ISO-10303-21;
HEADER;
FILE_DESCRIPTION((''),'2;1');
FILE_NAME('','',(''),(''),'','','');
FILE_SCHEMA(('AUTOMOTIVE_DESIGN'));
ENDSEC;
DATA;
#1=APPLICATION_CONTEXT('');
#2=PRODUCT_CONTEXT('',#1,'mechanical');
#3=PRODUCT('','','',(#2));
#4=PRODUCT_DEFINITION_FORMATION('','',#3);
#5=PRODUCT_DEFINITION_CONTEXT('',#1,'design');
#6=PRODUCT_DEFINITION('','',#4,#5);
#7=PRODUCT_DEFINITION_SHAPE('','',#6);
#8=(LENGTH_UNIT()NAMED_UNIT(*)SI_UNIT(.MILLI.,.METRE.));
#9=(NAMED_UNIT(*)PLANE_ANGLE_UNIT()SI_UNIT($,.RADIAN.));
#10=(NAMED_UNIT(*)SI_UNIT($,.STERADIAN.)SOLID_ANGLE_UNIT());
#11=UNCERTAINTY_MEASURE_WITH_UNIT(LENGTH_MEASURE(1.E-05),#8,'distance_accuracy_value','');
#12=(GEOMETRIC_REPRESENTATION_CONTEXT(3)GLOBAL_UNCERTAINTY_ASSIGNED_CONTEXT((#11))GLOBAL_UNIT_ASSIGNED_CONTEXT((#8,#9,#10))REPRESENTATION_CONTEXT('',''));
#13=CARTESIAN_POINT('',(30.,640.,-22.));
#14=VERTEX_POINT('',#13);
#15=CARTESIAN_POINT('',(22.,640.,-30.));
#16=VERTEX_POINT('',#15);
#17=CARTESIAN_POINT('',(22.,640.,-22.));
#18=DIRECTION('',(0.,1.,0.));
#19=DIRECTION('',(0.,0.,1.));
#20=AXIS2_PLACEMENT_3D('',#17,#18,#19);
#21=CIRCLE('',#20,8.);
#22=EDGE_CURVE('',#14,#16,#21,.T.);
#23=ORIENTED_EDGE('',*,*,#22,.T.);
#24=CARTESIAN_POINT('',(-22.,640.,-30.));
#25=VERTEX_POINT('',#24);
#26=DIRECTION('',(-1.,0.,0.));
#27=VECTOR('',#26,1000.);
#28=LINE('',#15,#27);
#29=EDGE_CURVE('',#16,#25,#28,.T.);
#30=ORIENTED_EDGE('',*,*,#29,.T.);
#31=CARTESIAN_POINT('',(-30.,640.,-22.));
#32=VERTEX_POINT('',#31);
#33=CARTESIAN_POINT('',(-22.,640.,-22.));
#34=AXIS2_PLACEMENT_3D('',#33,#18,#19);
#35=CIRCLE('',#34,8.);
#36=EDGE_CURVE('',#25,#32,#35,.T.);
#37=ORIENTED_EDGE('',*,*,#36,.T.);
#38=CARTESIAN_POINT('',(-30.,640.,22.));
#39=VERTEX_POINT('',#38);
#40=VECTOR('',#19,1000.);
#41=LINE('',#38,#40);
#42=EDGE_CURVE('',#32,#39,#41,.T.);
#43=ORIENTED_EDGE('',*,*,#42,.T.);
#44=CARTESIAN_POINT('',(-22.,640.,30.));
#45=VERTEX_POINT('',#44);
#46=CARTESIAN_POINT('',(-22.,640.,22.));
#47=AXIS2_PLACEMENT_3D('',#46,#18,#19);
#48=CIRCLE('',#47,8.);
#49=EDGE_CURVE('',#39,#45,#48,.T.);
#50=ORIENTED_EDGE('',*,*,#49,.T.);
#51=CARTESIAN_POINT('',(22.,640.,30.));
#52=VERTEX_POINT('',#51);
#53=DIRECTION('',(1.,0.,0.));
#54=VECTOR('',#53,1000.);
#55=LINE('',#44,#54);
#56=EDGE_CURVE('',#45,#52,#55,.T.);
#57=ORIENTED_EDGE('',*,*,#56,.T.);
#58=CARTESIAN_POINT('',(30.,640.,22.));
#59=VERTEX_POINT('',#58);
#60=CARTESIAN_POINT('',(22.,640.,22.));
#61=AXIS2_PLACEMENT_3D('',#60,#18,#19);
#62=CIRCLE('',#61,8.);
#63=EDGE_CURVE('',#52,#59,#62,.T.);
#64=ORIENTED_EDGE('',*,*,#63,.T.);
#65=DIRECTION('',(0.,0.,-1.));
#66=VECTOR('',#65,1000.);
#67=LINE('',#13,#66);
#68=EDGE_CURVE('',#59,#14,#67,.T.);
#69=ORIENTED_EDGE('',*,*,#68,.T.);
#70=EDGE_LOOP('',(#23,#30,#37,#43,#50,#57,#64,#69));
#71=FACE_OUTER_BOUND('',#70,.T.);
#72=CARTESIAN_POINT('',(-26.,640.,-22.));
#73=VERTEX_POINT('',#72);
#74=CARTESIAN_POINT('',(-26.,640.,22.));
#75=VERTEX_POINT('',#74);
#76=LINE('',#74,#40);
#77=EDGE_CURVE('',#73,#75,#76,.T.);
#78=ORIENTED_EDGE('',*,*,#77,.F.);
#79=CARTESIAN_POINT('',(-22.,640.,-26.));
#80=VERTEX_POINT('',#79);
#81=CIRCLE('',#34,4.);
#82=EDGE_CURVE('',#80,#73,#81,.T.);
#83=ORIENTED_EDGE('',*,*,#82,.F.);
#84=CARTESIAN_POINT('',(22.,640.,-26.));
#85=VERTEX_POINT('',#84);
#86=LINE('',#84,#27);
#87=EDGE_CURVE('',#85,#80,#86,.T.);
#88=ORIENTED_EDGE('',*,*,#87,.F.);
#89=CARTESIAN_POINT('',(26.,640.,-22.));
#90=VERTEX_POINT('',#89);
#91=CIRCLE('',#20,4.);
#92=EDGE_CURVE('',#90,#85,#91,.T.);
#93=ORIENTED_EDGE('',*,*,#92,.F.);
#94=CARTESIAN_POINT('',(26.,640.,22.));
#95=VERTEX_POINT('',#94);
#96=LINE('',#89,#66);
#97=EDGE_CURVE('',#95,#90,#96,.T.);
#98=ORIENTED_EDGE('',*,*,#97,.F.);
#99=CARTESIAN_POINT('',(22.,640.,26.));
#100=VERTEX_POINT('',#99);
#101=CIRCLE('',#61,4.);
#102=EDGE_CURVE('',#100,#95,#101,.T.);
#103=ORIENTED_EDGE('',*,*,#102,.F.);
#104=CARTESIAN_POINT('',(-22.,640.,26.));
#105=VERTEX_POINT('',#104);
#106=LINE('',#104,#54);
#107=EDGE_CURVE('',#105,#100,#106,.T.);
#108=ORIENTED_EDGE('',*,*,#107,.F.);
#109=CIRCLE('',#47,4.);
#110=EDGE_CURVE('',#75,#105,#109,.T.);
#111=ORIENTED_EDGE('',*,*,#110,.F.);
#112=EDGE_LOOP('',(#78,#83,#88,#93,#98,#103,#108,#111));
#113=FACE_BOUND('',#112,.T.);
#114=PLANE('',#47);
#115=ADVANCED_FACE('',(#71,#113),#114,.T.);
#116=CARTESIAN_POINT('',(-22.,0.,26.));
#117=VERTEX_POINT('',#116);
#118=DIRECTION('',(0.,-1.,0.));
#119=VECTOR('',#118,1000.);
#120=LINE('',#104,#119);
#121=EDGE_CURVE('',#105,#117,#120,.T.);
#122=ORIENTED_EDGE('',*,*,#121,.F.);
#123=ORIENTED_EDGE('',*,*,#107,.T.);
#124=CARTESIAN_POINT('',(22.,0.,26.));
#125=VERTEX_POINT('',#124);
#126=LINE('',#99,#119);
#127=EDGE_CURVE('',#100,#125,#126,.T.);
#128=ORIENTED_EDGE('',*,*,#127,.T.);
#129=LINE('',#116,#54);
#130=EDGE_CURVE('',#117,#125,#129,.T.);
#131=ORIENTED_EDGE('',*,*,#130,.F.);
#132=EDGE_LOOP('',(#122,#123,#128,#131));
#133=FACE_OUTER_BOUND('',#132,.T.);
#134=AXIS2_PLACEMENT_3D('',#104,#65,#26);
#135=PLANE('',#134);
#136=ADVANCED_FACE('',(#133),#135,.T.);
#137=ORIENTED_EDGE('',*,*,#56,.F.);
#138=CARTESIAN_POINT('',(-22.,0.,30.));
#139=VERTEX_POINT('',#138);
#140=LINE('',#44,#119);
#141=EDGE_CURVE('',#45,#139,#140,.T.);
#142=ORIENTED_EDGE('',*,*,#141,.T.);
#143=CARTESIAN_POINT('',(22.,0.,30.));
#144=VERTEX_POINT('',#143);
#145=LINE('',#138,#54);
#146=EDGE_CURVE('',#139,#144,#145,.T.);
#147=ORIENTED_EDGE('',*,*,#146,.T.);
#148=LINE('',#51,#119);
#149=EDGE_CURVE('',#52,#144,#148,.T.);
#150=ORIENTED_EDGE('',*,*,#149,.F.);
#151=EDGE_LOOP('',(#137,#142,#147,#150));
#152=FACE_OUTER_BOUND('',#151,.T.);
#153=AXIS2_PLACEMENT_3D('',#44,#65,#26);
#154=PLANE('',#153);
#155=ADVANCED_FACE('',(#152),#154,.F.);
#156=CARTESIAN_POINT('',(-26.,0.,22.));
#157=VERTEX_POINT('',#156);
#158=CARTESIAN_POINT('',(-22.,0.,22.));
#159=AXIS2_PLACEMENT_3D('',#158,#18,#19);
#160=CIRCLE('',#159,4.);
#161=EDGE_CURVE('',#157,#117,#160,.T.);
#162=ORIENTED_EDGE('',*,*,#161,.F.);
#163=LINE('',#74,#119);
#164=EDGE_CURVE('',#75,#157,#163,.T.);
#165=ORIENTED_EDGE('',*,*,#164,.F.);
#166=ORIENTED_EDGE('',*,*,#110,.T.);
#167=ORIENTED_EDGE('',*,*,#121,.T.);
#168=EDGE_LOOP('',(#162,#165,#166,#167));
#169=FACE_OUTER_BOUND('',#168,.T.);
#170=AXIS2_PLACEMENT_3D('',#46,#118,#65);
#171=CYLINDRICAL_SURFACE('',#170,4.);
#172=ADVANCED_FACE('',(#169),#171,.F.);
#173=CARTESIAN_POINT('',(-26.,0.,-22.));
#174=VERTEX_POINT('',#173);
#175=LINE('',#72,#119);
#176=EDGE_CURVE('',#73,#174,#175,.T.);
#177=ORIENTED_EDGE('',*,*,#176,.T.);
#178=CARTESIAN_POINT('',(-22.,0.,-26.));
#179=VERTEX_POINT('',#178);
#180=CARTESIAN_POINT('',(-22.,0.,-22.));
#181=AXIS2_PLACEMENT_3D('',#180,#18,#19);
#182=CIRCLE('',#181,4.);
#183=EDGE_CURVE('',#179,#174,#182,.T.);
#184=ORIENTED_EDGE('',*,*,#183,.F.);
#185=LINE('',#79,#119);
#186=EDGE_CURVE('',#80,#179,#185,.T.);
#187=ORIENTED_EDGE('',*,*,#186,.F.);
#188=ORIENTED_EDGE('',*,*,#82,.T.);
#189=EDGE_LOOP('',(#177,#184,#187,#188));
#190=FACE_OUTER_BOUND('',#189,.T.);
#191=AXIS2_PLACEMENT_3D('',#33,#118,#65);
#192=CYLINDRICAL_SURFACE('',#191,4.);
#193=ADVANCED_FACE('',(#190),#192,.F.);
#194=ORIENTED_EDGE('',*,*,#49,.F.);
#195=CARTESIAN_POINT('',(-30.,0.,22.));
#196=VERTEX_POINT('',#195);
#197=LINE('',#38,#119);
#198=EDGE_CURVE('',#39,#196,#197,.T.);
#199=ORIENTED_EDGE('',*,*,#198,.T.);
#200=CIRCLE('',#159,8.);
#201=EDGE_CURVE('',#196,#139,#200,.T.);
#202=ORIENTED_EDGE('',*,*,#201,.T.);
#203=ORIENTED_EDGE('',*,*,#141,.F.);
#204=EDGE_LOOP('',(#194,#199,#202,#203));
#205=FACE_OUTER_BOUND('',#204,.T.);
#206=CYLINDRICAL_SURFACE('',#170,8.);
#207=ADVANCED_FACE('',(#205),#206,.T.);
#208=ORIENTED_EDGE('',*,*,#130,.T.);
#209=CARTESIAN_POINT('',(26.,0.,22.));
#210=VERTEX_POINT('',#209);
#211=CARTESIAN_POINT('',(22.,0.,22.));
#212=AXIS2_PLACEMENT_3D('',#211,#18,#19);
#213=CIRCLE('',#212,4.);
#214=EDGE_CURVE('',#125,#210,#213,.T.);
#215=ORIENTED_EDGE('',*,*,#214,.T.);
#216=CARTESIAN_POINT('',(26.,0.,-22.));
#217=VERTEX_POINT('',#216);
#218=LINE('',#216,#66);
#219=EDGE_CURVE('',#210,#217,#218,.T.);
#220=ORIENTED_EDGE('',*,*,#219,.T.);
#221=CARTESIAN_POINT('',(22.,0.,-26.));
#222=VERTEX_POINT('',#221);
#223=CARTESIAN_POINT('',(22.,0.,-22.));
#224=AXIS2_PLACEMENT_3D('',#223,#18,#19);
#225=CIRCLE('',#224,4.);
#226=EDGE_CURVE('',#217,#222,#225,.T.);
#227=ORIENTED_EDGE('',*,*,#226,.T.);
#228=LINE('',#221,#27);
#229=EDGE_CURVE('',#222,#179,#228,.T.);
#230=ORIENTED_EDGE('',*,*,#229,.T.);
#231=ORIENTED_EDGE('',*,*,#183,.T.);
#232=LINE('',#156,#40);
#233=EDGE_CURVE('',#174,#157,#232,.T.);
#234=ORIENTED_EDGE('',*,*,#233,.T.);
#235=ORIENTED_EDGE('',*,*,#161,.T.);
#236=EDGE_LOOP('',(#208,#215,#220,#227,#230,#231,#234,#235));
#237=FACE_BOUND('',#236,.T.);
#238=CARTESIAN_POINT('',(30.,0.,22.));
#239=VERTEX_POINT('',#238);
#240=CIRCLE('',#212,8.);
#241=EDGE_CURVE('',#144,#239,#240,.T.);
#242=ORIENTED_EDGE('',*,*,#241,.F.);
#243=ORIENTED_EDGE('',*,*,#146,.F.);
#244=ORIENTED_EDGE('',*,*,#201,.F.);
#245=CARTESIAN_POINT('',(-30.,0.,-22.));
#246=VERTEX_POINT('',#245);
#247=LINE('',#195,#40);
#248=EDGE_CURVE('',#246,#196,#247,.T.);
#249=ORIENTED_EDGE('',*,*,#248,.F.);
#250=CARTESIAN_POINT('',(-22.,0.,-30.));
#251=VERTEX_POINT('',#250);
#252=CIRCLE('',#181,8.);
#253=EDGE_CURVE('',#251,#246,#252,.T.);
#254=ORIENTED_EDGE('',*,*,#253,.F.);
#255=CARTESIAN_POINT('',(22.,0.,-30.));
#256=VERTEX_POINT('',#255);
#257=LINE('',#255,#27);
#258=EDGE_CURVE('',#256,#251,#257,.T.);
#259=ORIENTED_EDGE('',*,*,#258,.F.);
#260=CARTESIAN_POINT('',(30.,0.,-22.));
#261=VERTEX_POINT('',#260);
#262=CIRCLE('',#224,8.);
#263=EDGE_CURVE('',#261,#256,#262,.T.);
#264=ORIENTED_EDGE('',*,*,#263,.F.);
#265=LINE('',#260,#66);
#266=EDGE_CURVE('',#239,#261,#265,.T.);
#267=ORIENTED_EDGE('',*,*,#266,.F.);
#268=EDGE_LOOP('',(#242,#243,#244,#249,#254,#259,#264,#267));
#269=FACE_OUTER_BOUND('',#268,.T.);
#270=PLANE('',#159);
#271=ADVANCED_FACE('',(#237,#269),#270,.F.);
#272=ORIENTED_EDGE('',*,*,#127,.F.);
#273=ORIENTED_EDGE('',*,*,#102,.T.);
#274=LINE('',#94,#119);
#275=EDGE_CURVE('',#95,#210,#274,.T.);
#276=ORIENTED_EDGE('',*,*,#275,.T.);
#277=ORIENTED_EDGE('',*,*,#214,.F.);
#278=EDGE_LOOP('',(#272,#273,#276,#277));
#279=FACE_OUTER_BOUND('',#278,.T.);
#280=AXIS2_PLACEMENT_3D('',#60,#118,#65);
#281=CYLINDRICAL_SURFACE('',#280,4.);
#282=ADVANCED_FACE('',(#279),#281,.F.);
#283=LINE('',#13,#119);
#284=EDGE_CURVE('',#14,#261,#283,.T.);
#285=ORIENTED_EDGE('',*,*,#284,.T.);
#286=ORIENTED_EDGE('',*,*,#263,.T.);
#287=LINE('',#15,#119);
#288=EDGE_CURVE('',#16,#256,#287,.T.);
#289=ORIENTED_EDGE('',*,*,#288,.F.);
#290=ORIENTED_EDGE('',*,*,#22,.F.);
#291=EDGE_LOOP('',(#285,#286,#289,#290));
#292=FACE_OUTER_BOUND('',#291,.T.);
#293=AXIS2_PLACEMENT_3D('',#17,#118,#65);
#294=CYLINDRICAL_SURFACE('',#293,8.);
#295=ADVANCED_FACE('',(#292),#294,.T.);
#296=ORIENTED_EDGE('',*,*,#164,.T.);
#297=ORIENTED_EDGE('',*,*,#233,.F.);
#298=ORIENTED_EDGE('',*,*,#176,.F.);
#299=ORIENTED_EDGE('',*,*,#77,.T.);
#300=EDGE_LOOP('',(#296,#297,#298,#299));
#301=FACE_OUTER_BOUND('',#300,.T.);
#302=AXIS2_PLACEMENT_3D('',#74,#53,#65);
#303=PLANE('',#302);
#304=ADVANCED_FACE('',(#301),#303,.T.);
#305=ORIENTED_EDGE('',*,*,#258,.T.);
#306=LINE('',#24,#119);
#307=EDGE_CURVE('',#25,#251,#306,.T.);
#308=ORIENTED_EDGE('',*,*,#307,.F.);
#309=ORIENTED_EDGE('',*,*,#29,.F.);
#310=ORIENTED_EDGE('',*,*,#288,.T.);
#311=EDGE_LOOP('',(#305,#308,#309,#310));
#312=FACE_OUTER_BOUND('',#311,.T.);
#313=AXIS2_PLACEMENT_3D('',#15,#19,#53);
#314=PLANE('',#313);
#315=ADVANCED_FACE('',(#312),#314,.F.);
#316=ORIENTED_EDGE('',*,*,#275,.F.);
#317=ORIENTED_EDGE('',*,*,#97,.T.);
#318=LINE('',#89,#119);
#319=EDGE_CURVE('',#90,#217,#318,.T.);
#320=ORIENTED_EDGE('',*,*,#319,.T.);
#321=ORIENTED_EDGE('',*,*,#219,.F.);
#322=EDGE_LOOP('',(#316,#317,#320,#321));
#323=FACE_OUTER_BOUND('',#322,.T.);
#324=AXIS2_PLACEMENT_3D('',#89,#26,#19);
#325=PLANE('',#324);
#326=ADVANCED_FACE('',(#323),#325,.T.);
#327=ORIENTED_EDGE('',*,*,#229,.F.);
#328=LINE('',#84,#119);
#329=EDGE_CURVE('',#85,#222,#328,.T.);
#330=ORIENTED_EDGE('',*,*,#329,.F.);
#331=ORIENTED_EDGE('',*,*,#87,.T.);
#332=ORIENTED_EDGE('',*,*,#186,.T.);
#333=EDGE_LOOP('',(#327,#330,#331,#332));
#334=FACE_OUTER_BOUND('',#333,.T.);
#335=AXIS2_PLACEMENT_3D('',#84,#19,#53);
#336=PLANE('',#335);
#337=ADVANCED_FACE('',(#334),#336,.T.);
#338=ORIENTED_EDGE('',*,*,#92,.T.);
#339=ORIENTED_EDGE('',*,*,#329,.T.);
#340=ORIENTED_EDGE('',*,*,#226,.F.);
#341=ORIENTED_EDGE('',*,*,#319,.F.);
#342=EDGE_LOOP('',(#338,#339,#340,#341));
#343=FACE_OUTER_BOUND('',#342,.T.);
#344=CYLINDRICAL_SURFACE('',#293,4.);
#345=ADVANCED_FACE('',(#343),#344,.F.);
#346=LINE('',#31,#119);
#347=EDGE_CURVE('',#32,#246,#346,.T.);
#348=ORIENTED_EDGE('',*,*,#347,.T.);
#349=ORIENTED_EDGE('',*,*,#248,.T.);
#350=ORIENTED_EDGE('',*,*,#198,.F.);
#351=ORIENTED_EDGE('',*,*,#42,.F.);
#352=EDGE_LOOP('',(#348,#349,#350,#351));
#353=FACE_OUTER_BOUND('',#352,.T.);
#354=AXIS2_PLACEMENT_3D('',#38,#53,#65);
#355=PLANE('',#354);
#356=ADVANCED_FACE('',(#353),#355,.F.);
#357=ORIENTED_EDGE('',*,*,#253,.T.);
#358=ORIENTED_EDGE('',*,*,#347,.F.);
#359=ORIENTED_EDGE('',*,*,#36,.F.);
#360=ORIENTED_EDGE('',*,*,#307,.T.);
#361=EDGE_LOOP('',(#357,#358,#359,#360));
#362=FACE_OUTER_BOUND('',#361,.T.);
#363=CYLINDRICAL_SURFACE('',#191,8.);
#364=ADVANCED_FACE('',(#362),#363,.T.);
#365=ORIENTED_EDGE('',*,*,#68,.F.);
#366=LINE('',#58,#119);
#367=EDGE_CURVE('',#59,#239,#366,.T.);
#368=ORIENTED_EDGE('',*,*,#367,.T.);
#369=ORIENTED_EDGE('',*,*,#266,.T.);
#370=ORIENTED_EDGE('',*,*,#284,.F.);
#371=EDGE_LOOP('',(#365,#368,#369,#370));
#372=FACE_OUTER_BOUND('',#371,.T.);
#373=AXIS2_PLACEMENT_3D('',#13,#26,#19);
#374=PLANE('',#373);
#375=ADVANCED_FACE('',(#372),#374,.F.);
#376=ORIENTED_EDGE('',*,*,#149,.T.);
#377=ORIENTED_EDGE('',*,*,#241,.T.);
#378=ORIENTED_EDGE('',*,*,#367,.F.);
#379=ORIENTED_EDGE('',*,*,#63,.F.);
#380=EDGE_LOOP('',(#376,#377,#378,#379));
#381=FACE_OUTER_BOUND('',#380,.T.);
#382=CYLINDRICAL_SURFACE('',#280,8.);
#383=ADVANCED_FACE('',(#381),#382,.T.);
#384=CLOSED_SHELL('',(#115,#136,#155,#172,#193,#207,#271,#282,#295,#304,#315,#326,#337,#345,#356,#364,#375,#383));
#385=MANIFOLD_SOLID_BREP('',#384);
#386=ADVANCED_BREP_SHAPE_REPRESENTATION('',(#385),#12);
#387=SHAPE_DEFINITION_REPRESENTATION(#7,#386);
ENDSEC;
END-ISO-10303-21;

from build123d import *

# Parameters (mm, degrees)
GB_T_6728_2002_SQUARE_HOLLOW_SECTION_60_DEPTH = 640


with BuildPart() as part:
    # Sketch1 → GB/T 6728-2002 square hollow section 60×60×4(1) (new body)
    with BuildSketch(Plane(origin=(0, 0, 0), x_dir=(-1, 0, 0), z_dir=(0, 1, 0))):
        with BuildLine():
            Line((-22, -30), (22, -30))
            ThreePointArc((22, -30), (27.656854249, -27.656854249), (30, -22))
            Line((30, -22), (30, 22))
            ThreePointArc((30, 22), (27.656854249, 27.656854249), (22, 30))
            Line((22, 30), (-22, 30))
            ThreePointArc((-22, 30), (-27.656854249, 27.656854249), (-30, 22))
            Line((-30, 22), (-30, -22))
            ThreePointArc((-30, -22), (-27.656854249, -27.656854249), (-22, -30))
        make_face()
        with BuildLine():
            Line((-22, -26), (22, -26))
            ThreePointArc((22, -26), (24.828427125, -24.828427125), (26, -22))
            Line((26, -22), (26, 22))
            ThreePointArc((26, 22), (24.828427125, 24.828427125), (22, 26))
            Line((22, 26), (-22, 26))
            ThreePointArc((-22, 26), (-24.828427125, 24.828427125), (-26, 22))
            Line((-26, 22), (-26, -22))
            ThreePointArc((-26, -22), (-24.828427125, -24.828427125), (-22, -26))
        make_face(mode=Mode.SUBTRACT)
    extrude(amount=GB_T_6728_2002_SQUARE_HOLLOW_SECTION_60_DEPTH)


solid = part.part
